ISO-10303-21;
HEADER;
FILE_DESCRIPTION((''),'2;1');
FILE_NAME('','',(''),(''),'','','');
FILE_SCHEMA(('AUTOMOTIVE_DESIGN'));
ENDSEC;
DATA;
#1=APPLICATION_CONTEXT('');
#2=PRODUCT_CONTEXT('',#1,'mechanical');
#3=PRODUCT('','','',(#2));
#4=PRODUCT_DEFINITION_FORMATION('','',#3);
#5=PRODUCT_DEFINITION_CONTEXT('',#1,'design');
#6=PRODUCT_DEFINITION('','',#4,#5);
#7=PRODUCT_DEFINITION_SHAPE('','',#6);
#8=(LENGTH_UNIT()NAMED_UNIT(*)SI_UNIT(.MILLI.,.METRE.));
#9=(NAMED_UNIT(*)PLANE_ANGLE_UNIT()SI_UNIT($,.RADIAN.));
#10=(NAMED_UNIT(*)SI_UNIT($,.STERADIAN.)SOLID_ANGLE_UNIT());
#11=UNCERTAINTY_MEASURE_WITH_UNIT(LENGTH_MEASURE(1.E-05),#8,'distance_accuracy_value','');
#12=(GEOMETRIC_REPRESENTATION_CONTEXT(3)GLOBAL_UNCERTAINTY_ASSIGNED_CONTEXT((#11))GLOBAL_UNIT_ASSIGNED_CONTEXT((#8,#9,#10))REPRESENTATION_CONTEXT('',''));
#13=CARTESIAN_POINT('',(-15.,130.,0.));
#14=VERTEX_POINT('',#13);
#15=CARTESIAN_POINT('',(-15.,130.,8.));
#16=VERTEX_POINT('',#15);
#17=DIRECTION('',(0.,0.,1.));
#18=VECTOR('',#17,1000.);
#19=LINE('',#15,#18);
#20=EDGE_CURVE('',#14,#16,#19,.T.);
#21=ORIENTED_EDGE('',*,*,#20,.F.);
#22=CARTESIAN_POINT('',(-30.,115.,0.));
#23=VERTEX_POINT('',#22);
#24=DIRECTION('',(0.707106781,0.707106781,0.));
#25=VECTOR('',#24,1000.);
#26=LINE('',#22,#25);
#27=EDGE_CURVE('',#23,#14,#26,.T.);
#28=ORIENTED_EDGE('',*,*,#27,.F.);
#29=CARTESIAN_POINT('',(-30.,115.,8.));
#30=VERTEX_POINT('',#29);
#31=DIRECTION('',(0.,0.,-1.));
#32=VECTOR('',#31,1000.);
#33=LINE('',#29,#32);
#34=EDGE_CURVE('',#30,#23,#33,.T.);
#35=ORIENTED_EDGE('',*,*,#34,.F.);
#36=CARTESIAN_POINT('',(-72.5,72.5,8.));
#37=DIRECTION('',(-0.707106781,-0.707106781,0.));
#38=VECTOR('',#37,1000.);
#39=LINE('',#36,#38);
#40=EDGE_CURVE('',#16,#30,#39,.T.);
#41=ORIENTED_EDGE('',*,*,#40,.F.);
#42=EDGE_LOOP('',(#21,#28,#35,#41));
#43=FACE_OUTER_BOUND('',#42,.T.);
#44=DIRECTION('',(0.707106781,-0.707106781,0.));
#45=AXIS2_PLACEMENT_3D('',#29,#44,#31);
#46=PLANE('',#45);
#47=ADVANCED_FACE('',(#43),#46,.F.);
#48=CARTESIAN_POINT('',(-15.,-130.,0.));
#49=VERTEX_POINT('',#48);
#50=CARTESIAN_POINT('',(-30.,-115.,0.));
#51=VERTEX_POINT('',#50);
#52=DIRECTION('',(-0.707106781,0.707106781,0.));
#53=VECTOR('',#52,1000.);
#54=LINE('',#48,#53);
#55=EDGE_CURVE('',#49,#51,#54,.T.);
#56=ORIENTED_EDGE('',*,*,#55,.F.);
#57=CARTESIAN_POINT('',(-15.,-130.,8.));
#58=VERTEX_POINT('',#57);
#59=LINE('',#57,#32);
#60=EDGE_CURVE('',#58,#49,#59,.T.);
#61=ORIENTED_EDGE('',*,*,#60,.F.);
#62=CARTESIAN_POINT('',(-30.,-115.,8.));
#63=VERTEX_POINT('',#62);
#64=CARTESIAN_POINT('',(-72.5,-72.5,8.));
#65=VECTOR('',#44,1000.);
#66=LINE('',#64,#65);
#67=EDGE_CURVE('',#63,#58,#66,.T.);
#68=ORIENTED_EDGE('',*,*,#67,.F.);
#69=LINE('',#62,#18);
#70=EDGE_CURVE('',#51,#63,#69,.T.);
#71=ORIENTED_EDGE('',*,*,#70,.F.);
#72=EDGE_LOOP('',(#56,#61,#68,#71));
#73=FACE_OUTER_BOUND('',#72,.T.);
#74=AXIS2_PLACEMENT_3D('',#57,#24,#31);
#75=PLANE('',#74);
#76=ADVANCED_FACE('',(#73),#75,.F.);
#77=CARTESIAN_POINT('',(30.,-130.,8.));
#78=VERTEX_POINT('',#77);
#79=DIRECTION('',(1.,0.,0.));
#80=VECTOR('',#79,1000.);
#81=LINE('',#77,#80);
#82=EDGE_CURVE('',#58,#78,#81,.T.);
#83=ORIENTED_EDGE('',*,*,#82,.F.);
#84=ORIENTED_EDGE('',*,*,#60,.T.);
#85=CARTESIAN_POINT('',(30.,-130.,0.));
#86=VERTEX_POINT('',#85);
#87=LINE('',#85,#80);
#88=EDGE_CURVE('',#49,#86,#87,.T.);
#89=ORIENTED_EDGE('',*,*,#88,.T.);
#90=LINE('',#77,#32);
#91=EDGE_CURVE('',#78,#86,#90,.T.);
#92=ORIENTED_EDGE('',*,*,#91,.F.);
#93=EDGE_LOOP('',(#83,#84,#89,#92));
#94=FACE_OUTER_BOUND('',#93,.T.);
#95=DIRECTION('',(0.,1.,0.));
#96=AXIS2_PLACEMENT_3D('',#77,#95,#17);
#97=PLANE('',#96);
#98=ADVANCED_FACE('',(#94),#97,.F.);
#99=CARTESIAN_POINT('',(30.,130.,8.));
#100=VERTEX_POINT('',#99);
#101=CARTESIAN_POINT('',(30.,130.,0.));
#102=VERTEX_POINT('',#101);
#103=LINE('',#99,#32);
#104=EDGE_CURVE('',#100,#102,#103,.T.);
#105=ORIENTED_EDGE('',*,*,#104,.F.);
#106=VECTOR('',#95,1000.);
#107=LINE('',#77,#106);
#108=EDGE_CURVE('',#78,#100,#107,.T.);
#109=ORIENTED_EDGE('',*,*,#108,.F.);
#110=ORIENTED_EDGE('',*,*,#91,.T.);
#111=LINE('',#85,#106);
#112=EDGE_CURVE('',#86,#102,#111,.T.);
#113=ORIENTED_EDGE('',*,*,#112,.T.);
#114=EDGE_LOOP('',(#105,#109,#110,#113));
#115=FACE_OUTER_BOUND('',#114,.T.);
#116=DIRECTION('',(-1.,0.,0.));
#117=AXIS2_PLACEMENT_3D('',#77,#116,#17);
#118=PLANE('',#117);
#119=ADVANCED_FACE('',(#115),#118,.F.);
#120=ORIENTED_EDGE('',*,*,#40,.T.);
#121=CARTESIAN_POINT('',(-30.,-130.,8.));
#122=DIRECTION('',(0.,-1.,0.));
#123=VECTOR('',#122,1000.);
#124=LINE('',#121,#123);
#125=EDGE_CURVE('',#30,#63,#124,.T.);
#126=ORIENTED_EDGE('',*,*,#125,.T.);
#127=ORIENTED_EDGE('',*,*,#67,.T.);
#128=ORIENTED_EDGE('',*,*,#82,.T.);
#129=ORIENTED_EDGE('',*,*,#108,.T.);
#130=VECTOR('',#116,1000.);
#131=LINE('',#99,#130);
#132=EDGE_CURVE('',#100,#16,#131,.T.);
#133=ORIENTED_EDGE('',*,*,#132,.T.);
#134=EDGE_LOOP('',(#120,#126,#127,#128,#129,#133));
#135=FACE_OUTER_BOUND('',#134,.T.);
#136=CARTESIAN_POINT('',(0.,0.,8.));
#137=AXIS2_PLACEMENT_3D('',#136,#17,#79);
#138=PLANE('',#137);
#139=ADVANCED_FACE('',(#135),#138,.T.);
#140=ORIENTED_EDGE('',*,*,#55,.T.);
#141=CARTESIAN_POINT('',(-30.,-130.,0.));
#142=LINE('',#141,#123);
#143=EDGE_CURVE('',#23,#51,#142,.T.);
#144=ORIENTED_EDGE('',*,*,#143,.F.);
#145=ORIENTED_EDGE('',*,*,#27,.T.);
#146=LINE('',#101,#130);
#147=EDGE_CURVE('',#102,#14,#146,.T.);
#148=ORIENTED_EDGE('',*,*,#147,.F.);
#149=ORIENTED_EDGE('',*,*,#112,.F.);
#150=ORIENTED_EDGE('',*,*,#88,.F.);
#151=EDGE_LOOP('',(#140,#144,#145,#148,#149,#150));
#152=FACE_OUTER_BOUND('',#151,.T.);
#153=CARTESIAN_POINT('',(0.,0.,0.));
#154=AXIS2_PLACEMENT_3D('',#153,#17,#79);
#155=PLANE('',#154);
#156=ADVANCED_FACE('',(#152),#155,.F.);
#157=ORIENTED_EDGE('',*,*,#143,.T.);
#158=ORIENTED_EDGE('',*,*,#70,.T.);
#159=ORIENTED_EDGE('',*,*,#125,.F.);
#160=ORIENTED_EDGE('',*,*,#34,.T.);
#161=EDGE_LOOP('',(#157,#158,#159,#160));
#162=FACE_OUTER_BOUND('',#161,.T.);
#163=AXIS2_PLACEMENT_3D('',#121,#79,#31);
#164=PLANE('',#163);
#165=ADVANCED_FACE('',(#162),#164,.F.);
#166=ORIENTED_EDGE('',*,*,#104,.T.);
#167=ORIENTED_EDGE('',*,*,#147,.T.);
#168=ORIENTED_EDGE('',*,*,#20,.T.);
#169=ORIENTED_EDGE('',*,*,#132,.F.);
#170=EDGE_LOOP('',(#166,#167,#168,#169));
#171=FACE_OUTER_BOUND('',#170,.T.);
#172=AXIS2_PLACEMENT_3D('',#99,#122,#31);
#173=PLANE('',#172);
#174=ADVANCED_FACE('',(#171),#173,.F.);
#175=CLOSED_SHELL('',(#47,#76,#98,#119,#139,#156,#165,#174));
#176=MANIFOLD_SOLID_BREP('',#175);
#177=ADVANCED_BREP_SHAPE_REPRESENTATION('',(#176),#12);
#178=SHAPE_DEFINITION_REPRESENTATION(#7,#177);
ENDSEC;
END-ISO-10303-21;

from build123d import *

# Parameters (mm, degrees)
SKETCH1_W           = 60
SKETCH1_H           = 260
BOSS_EXTRUDE1_DEPTH = 8
CHAMFER1_SIZE       = 15


with BuildPart() as part:
    # Sketch1 → Boss-Extrude1 (new body)
    with BuildSketch(Plane.XY):
        Rectangle(SKETCH1_W, SKETCH1_H)
    extrude(amount=BOSS_EXTRUDE1_DEPTH)

    # Chamfer1
    chamfer1_edges = [part.edges().sort_by_distance(p)[0] for p in [
        (-30, 130, 4),
        (-30, -130, 4),
    ]]
    chamfer(chamfer1_edges, length=CHAMFER1_SIZE)


solid = part.part
